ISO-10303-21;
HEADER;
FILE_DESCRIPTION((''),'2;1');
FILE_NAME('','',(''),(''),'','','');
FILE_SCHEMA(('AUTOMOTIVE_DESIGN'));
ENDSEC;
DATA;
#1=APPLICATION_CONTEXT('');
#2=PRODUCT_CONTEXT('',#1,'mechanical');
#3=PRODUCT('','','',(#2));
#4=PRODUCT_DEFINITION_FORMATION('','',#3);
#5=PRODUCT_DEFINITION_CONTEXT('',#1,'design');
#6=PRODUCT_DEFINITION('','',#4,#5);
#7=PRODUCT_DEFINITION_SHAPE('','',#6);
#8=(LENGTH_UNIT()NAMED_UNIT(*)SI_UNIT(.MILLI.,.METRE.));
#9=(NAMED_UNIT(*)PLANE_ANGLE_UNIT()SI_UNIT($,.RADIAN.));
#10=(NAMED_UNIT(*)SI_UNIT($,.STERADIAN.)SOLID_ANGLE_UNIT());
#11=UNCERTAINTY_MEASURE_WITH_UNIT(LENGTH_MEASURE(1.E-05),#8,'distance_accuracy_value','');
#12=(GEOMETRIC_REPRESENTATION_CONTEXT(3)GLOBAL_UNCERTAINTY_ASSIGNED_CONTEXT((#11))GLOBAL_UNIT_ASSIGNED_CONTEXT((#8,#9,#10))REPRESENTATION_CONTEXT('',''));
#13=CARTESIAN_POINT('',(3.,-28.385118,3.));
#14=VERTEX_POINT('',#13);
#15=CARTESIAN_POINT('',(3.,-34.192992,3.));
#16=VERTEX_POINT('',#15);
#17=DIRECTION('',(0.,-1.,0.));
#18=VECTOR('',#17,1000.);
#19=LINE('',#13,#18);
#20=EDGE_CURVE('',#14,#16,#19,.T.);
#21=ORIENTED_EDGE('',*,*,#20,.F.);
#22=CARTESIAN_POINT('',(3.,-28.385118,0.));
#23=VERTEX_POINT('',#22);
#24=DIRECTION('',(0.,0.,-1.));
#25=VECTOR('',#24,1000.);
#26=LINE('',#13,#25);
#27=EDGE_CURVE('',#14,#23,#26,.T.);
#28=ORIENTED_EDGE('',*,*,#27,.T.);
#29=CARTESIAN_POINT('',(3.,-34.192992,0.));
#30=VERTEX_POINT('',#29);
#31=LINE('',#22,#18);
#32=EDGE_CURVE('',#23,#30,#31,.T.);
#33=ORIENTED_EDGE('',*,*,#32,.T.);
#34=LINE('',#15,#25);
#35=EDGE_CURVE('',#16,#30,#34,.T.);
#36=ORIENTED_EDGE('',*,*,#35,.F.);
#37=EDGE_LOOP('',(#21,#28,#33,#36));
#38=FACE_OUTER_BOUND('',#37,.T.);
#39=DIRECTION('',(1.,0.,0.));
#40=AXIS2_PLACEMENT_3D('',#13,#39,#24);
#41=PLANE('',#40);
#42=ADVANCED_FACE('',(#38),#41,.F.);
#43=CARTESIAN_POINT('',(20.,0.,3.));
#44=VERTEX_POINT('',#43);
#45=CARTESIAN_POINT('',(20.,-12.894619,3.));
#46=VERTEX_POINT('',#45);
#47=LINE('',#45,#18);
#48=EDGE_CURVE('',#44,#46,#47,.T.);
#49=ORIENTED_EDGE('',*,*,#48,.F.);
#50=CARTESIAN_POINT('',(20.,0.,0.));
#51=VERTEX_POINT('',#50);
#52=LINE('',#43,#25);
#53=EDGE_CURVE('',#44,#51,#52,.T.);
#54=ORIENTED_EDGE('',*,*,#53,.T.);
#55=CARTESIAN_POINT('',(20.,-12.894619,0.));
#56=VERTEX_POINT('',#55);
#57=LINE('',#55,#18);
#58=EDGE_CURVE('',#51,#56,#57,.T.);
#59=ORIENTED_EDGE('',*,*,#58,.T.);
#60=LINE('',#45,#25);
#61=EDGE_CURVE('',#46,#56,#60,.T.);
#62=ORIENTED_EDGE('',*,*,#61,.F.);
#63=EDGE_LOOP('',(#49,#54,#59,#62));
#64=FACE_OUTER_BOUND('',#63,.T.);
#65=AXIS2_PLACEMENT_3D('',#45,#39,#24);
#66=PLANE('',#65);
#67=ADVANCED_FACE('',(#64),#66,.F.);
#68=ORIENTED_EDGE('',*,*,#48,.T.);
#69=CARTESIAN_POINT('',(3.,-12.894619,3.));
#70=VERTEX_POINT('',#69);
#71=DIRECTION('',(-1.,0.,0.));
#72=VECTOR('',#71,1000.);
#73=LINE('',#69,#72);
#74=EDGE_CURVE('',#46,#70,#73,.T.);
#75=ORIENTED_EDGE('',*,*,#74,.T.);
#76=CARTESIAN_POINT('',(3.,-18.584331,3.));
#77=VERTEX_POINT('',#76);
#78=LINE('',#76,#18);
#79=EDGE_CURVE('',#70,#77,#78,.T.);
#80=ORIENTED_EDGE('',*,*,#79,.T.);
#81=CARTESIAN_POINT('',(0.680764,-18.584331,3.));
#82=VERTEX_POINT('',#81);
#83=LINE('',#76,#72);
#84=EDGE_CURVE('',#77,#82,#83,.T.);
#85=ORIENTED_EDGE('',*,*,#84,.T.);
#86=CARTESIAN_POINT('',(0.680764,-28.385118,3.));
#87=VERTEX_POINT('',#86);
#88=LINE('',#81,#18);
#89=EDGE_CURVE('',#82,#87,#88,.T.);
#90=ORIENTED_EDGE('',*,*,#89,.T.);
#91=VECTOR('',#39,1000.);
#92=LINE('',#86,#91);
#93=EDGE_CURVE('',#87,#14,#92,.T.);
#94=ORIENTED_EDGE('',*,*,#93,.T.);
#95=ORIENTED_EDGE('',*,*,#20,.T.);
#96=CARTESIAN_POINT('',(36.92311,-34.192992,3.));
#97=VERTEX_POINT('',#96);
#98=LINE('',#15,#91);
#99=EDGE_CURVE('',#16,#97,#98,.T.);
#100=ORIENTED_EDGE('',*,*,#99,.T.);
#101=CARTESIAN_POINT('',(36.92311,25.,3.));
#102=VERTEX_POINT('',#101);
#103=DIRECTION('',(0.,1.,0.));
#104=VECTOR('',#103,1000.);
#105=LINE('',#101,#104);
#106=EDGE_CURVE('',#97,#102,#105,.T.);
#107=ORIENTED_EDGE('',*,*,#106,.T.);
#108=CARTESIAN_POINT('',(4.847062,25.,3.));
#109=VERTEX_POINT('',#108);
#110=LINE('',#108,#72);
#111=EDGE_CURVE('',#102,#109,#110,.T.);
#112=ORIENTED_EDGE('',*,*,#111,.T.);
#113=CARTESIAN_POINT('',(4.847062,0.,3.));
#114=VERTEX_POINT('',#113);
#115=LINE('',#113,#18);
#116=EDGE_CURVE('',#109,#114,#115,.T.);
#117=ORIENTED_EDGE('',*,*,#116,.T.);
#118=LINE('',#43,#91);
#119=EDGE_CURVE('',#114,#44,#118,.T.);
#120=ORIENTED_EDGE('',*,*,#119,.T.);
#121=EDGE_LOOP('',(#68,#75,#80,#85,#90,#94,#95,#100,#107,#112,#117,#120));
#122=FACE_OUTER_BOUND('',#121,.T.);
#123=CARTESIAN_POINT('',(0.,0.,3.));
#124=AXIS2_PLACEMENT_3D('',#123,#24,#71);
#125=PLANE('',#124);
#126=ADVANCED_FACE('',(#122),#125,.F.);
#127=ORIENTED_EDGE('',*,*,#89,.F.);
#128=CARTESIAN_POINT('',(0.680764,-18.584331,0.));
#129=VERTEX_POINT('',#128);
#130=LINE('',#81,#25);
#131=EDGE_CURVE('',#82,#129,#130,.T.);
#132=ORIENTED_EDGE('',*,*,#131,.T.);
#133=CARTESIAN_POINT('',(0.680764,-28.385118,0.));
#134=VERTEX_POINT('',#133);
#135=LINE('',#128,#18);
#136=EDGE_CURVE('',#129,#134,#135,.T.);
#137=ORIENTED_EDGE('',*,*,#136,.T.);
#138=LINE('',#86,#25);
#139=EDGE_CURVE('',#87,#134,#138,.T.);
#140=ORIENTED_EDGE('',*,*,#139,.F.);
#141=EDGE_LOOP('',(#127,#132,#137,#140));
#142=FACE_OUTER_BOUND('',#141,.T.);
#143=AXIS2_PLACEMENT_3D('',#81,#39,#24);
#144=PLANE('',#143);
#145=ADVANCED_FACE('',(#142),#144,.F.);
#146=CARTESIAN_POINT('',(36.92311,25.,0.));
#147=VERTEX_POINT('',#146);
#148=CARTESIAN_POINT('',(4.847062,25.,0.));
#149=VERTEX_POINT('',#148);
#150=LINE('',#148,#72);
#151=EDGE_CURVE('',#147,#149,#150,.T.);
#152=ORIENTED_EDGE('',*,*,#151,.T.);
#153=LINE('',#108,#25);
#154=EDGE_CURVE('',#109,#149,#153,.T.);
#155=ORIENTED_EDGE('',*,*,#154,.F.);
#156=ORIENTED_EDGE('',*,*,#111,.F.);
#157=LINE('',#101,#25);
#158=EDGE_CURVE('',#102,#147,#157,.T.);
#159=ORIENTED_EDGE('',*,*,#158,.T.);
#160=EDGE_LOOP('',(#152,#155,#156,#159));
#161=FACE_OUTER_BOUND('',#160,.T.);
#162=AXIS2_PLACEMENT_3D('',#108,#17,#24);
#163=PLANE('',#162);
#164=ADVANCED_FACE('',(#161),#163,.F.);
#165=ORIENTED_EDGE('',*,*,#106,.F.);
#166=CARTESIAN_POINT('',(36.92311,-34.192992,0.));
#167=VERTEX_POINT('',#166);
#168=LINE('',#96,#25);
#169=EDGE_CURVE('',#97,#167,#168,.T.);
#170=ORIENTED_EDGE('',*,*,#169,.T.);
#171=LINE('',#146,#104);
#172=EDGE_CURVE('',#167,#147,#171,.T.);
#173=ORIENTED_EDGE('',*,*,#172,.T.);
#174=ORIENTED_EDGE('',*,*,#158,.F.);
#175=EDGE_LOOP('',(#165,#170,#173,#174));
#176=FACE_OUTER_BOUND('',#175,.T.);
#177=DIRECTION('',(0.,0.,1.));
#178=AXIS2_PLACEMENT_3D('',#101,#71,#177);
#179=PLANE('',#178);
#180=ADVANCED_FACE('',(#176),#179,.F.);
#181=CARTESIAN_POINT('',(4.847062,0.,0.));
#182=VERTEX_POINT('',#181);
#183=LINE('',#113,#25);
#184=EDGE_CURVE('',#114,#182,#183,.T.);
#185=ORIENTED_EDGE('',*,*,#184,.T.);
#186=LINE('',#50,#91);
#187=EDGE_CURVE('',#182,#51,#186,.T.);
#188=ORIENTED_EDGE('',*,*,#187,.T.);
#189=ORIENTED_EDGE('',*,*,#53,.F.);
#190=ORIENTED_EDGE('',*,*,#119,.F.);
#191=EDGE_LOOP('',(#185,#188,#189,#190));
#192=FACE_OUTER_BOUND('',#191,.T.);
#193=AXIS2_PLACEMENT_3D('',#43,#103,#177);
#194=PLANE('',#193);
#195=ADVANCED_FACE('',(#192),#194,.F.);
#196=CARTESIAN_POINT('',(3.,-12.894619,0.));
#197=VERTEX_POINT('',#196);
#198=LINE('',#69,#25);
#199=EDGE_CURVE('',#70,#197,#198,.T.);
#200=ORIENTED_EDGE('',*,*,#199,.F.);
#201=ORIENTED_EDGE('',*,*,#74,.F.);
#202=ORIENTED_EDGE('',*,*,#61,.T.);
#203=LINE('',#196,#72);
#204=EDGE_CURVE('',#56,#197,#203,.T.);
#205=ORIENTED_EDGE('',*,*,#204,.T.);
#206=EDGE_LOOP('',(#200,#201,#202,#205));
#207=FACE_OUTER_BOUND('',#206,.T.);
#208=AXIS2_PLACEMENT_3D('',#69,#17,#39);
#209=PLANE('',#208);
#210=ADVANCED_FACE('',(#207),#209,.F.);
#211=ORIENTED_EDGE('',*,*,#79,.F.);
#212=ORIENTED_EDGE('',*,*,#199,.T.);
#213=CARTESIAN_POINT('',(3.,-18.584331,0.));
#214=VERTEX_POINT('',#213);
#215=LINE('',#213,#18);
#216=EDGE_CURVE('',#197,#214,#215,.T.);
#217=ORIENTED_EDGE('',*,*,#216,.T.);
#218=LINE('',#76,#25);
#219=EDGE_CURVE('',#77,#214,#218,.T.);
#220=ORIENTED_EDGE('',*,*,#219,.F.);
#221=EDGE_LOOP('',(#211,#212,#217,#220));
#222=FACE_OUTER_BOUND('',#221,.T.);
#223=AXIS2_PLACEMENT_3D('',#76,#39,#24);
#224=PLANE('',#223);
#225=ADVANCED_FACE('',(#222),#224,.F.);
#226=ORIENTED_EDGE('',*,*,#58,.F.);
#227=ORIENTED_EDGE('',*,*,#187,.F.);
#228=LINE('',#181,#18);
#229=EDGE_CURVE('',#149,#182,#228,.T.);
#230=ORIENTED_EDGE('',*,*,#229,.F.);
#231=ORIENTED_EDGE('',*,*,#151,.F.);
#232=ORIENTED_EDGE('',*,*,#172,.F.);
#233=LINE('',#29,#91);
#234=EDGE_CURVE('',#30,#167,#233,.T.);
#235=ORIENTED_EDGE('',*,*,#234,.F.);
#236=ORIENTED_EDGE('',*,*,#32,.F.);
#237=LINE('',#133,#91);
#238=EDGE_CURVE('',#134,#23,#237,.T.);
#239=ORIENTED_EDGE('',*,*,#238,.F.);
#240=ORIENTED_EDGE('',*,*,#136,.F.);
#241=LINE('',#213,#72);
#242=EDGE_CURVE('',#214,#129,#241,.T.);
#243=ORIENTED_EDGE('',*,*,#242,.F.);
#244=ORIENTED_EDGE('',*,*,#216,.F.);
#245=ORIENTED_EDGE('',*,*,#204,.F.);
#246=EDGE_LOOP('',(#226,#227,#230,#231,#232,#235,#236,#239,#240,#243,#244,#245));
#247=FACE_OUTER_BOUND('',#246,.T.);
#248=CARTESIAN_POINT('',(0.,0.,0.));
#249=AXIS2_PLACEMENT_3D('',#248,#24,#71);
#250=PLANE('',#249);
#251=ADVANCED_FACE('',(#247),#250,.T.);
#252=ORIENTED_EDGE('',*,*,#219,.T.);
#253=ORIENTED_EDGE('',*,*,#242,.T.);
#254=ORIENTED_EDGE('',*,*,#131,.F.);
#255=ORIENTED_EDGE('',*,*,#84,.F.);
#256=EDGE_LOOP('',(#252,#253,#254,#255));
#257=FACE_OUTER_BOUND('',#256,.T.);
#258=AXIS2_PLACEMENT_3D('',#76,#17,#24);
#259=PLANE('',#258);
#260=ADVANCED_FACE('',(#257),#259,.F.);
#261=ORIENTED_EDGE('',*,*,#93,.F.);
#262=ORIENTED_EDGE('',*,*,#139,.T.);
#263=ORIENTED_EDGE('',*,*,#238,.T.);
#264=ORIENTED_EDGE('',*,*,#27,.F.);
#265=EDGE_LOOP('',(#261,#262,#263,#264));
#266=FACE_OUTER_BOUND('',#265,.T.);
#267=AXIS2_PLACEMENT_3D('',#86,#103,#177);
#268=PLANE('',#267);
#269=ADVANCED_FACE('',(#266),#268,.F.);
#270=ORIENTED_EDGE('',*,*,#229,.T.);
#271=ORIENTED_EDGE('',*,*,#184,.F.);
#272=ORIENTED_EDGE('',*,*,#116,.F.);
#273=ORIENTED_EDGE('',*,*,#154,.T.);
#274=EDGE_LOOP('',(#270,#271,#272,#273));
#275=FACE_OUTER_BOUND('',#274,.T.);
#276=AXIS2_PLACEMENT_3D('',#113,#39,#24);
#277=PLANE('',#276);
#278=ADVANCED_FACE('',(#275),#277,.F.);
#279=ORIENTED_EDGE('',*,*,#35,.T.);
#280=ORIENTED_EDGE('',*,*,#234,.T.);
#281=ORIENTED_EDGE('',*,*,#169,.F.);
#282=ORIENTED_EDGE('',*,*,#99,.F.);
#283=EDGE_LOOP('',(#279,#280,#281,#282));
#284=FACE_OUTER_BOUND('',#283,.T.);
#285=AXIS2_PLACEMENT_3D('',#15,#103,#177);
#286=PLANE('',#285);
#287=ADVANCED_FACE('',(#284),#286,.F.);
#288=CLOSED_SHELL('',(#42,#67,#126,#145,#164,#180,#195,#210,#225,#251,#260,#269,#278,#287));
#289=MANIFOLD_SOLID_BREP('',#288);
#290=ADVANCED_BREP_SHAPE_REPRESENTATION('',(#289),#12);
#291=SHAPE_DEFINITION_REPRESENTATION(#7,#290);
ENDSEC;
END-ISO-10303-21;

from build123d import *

# Parameters (mm, degrees)
BOSS_EXTRUDE1_DEPTH = 3


with BuildPart() as part:
    # Sketch1 → Boss-Extrude1 (new body)
    with BuildSketch(Plane.XY):
        Polygon((3, -18.58433147), (0.680763745, -18.58433147), (0.680763745, -28.385118219), (3, -28.385118219), (3, -34.192991848), (36.923110286, -34.192991848), (36.923110286, 25), (4.847061595, 25), (4.847061595, 0), (20, 0), (20, -12.894618578), (3, -12.894618578), align=None)
    extrude(amount=BOSS_EXTRUDE1_DEPTH)


solid = part.part
